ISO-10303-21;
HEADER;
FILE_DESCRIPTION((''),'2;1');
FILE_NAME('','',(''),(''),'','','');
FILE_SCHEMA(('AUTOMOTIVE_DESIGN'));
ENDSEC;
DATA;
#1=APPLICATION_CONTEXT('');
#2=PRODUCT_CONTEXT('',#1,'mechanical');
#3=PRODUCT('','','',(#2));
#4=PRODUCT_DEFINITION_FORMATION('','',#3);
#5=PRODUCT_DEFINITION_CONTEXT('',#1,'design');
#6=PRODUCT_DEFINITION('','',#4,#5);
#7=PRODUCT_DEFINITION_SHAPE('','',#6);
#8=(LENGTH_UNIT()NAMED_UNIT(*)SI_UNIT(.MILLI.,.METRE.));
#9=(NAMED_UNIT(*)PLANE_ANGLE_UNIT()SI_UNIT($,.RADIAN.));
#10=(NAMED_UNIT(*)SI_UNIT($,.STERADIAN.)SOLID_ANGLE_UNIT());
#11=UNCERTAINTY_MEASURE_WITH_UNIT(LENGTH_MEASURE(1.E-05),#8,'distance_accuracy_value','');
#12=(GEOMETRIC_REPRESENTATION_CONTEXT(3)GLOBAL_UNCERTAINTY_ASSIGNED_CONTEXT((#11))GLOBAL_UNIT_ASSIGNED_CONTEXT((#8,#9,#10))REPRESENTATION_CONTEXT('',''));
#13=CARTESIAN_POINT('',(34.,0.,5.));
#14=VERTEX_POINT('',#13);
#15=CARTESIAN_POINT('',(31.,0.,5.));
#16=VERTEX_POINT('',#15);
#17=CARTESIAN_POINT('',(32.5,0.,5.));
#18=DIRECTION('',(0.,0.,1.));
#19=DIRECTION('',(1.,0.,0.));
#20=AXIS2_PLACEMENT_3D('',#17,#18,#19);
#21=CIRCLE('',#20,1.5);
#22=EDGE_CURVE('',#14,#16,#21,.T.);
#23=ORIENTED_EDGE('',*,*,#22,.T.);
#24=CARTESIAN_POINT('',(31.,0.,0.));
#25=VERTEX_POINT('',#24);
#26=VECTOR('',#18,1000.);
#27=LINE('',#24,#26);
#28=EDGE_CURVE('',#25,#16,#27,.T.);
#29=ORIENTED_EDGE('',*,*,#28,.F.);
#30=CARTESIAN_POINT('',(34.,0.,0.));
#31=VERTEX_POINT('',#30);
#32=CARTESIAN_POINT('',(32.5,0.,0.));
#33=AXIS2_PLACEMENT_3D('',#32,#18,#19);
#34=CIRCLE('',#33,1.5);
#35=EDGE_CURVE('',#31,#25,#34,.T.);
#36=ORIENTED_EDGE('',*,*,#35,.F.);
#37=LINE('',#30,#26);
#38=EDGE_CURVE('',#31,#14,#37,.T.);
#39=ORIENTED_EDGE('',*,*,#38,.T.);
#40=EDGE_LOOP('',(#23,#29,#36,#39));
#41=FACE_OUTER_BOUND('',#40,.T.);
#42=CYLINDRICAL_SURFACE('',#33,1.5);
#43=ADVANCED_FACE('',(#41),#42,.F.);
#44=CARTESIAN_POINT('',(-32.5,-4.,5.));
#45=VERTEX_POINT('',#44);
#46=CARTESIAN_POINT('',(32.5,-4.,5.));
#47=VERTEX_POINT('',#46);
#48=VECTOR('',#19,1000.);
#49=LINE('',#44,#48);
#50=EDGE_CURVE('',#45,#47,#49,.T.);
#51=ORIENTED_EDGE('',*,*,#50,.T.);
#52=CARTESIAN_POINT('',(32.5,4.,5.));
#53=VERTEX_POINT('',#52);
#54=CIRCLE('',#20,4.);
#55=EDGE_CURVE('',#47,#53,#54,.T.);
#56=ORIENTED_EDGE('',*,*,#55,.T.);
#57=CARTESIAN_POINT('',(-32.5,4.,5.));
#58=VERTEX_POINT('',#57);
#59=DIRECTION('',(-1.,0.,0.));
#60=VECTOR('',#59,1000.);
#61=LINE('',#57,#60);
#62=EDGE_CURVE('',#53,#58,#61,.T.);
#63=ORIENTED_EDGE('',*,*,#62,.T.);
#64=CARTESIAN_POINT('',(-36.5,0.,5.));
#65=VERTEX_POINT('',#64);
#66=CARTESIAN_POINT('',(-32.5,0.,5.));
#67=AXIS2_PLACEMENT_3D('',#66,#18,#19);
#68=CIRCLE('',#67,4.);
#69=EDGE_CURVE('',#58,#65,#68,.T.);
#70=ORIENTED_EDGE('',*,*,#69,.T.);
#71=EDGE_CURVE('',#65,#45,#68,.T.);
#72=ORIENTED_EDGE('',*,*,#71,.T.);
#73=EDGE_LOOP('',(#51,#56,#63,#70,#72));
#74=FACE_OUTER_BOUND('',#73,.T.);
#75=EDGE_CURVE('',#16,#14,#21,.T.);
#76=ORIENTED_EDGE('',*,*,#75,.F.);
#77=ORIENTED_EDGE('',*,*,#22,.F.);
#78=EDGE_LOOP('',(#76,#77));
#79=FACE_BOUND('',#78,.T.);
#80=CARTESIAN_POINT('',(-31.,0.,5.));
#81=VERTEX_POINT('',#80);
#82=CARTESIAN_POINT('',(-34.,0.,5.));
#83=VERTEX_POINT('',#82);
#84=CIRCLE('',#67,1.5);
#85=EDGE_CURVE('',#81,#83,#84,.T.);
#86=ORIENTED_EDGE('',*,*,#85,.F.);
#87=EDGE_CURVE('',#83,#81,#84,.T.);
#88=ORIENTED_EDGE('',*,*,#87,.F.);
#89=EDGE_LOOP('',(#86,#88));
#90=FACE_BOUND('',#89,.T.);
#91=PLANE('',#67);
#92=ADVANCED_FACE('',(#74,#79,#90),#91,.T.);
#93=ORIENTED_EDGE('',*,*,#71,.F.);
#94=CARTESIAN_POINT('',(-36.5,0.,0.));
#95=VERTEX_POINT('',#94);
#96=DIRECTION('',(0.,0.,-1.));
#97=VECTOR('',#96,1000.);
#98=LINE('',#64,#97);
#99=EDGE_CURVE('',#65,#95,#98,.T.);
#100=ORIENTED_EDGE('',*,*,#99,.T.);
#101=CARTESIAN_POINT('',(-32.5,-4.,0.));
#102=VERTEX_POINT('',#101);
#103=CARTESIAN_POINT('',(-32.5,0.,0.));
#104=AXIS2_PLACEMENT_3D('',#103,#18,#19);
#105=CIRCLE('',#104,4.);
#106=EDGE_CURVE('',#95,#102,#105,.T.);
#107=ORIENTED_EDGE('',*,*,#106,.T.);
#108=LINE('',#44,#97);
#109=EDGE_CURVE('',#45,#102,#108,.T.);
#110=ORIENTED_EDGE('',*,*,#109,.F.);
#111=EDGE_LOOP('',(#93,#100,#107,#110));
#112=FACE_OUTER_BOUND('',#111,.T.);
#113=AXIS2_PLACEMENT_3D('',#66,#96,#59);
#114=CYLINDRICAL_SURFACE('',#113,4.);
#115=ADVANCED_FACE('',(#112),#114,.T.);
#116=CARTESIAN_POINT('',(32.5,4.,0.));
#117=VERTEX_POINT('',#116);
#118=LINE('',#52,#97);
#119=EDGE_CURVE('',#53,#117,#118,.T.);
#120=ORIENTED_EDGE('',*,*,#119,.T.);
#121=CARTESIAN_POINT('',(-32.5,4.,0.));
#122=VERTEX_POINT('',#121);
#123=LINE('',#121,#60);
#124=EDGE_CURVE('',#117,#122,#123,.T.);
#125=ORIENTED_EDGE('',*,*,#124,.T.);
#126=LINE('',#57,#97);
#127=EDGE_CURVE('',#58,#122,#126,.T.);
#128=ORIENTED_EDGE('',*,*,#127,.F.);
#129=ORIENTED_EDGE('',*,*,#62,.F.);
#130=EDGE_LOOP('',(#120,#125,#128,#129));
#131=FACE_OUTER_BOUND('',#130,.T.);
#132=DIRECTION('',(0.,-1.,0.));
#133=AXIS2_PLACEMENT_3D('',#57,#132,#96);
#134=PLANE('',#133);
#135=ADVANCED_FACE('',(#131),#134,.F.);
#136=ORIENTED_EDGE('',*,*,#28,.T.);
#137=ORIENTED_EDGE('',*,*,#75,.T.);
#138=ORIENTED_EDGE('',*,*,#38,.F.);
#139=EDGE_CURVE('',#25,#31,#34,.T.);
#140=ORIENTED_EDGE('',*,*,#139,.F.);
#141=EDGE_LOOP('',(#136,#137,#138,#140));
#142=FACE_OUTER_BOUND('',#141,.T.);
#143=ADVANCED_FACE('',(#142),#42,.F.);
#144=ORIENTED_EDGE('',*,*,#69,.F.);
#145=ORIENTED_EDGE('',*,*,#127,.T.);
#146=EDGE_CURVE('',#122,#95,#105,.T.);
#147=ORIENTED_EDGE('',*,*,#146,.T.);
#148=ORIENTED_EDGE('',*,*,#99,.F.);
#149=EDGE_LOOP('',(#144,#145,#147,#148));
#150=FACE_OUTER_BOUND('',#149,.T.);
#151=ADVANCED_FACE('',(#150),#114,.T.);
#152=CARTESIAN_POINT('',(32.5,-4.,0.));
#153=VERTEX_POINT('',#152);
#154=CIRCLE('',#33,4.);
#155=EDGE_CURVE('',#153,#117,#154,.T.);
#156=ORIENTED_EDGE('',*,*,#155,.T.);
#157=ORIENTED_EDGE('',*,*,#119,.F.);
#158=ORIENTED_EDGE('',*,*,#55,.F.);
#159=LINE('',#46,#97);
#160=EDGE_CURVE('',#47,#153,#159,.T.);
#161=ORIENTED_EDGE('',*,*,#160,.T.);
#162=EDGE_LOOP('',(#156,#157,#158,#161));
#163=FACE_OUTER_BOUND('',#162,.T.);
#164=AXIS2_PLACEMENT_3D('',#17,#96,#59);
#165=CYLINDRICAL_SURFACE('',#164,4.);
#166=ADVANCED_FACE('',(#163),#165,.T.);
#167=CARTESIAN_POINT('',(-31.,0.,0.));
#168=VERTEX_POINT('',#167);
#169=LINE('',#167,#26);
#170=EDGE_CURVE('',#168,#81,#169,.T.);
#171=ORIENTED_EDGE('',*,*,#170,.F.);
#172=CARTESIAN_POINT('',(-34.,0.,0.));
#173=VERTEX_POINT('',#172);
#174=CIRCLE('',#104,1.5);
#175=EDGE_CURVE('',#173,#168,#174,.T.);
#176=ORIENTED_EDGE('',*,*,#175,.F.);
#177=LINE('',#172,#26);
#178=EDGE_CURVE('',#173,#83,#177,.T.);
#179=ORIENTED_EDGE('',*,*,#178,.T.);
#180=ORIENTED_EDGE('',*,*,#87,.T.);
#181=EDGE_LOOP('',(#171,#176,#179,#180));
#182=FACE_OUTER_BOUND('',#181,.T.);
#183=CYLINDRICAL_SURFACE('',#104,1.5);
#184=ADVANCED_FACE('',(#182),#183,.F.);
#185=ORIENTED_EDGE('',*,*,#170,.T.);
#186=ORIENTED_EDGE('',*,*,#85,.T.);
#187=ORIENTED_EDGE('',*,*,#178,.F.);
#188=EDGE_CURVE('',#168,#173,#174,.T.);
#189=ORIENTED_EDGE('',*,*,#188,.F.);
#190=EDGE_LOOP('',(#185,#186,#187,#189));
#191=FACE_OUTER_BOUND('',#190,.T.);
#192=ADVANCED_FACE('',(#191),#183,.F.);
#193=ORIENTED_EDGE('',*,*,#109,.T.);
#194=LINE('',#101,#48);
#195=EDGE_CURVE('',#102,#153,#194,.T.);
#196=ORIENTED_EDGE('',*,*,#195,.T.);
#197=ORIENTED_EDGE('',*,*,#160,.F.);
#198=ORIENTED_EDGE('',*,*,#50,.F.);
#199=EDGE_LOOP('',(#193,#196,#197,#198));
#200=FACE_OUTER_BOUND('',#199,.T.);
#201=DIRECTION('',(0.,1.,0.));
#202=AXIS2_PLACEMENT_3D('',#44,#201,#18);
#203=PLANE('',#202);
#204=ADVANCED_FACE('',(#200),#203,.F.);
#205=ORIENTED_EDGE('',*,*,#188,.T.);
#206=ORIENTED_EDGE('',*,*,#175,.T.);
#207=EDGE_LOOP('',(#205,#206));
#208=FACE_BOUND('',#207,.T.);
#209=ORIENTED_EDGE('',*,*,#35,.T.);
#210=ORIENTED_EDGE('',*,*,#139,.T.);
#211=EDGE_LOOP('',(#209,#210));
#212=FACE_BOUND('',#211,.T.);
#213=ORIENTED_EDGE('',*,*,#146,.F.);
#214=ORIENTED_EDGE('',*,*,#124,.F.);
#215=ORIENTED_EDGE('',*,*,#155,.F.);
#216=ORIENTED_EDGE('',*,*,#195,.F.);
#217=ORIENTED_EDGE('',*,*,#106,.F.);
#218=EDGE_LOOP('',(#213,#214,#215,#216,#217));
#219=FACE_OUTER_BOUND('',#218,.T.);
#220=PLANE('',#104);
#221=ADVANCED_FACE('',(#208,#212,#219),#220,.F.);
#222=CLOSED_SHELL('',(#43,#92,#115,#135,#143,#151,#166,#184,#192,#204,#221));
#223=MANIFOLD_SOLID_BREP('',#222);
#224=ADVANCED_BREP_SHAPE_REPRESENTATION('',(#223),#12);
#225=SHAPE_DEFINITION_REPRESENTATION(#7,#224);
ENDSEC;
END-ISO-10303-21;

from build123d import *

# Parameters (mm, degrees)
BOSS_EXTRUDE1_DEPTH = 5
SKETCH3_R           = 1.5
CUT_EXTRUDE1_DEPTH  = 38.057387927


with BuildPart() as part:
    # Sketch1 → Boss-Extrude1 (new body)
    with BuildSketch(Plane.XY):
        with BuildLine():
            Line((-32.5, 4), (32.5, 4))
            ThreePointArc((32.5, 4), (36.5, 0), (32.5, -4))
            Line((32.5, -4), (-32.5, -4))
            ThreePointArc((-32.5, -4), (-36.5, 0), (-32.5, 4))
        make_face()
    extrude(amount=BOSS_EXTRUDE1_DEPTH)

    # Sketch3 → Cut-Extrude1 (cut, through all)
    with BuildSketch(Plane.XY.offset(5)):
        with Locations((-32.5, 0)):
            Circle(SKETCH3_R)
        with Locations((32.5, 0)):
            Circle(SKETCH3_R)
    extrude(amount=-CUT_EXTRUDE1_DEPTH, mode=Mode.SUBTRACT)


solid = part.part
